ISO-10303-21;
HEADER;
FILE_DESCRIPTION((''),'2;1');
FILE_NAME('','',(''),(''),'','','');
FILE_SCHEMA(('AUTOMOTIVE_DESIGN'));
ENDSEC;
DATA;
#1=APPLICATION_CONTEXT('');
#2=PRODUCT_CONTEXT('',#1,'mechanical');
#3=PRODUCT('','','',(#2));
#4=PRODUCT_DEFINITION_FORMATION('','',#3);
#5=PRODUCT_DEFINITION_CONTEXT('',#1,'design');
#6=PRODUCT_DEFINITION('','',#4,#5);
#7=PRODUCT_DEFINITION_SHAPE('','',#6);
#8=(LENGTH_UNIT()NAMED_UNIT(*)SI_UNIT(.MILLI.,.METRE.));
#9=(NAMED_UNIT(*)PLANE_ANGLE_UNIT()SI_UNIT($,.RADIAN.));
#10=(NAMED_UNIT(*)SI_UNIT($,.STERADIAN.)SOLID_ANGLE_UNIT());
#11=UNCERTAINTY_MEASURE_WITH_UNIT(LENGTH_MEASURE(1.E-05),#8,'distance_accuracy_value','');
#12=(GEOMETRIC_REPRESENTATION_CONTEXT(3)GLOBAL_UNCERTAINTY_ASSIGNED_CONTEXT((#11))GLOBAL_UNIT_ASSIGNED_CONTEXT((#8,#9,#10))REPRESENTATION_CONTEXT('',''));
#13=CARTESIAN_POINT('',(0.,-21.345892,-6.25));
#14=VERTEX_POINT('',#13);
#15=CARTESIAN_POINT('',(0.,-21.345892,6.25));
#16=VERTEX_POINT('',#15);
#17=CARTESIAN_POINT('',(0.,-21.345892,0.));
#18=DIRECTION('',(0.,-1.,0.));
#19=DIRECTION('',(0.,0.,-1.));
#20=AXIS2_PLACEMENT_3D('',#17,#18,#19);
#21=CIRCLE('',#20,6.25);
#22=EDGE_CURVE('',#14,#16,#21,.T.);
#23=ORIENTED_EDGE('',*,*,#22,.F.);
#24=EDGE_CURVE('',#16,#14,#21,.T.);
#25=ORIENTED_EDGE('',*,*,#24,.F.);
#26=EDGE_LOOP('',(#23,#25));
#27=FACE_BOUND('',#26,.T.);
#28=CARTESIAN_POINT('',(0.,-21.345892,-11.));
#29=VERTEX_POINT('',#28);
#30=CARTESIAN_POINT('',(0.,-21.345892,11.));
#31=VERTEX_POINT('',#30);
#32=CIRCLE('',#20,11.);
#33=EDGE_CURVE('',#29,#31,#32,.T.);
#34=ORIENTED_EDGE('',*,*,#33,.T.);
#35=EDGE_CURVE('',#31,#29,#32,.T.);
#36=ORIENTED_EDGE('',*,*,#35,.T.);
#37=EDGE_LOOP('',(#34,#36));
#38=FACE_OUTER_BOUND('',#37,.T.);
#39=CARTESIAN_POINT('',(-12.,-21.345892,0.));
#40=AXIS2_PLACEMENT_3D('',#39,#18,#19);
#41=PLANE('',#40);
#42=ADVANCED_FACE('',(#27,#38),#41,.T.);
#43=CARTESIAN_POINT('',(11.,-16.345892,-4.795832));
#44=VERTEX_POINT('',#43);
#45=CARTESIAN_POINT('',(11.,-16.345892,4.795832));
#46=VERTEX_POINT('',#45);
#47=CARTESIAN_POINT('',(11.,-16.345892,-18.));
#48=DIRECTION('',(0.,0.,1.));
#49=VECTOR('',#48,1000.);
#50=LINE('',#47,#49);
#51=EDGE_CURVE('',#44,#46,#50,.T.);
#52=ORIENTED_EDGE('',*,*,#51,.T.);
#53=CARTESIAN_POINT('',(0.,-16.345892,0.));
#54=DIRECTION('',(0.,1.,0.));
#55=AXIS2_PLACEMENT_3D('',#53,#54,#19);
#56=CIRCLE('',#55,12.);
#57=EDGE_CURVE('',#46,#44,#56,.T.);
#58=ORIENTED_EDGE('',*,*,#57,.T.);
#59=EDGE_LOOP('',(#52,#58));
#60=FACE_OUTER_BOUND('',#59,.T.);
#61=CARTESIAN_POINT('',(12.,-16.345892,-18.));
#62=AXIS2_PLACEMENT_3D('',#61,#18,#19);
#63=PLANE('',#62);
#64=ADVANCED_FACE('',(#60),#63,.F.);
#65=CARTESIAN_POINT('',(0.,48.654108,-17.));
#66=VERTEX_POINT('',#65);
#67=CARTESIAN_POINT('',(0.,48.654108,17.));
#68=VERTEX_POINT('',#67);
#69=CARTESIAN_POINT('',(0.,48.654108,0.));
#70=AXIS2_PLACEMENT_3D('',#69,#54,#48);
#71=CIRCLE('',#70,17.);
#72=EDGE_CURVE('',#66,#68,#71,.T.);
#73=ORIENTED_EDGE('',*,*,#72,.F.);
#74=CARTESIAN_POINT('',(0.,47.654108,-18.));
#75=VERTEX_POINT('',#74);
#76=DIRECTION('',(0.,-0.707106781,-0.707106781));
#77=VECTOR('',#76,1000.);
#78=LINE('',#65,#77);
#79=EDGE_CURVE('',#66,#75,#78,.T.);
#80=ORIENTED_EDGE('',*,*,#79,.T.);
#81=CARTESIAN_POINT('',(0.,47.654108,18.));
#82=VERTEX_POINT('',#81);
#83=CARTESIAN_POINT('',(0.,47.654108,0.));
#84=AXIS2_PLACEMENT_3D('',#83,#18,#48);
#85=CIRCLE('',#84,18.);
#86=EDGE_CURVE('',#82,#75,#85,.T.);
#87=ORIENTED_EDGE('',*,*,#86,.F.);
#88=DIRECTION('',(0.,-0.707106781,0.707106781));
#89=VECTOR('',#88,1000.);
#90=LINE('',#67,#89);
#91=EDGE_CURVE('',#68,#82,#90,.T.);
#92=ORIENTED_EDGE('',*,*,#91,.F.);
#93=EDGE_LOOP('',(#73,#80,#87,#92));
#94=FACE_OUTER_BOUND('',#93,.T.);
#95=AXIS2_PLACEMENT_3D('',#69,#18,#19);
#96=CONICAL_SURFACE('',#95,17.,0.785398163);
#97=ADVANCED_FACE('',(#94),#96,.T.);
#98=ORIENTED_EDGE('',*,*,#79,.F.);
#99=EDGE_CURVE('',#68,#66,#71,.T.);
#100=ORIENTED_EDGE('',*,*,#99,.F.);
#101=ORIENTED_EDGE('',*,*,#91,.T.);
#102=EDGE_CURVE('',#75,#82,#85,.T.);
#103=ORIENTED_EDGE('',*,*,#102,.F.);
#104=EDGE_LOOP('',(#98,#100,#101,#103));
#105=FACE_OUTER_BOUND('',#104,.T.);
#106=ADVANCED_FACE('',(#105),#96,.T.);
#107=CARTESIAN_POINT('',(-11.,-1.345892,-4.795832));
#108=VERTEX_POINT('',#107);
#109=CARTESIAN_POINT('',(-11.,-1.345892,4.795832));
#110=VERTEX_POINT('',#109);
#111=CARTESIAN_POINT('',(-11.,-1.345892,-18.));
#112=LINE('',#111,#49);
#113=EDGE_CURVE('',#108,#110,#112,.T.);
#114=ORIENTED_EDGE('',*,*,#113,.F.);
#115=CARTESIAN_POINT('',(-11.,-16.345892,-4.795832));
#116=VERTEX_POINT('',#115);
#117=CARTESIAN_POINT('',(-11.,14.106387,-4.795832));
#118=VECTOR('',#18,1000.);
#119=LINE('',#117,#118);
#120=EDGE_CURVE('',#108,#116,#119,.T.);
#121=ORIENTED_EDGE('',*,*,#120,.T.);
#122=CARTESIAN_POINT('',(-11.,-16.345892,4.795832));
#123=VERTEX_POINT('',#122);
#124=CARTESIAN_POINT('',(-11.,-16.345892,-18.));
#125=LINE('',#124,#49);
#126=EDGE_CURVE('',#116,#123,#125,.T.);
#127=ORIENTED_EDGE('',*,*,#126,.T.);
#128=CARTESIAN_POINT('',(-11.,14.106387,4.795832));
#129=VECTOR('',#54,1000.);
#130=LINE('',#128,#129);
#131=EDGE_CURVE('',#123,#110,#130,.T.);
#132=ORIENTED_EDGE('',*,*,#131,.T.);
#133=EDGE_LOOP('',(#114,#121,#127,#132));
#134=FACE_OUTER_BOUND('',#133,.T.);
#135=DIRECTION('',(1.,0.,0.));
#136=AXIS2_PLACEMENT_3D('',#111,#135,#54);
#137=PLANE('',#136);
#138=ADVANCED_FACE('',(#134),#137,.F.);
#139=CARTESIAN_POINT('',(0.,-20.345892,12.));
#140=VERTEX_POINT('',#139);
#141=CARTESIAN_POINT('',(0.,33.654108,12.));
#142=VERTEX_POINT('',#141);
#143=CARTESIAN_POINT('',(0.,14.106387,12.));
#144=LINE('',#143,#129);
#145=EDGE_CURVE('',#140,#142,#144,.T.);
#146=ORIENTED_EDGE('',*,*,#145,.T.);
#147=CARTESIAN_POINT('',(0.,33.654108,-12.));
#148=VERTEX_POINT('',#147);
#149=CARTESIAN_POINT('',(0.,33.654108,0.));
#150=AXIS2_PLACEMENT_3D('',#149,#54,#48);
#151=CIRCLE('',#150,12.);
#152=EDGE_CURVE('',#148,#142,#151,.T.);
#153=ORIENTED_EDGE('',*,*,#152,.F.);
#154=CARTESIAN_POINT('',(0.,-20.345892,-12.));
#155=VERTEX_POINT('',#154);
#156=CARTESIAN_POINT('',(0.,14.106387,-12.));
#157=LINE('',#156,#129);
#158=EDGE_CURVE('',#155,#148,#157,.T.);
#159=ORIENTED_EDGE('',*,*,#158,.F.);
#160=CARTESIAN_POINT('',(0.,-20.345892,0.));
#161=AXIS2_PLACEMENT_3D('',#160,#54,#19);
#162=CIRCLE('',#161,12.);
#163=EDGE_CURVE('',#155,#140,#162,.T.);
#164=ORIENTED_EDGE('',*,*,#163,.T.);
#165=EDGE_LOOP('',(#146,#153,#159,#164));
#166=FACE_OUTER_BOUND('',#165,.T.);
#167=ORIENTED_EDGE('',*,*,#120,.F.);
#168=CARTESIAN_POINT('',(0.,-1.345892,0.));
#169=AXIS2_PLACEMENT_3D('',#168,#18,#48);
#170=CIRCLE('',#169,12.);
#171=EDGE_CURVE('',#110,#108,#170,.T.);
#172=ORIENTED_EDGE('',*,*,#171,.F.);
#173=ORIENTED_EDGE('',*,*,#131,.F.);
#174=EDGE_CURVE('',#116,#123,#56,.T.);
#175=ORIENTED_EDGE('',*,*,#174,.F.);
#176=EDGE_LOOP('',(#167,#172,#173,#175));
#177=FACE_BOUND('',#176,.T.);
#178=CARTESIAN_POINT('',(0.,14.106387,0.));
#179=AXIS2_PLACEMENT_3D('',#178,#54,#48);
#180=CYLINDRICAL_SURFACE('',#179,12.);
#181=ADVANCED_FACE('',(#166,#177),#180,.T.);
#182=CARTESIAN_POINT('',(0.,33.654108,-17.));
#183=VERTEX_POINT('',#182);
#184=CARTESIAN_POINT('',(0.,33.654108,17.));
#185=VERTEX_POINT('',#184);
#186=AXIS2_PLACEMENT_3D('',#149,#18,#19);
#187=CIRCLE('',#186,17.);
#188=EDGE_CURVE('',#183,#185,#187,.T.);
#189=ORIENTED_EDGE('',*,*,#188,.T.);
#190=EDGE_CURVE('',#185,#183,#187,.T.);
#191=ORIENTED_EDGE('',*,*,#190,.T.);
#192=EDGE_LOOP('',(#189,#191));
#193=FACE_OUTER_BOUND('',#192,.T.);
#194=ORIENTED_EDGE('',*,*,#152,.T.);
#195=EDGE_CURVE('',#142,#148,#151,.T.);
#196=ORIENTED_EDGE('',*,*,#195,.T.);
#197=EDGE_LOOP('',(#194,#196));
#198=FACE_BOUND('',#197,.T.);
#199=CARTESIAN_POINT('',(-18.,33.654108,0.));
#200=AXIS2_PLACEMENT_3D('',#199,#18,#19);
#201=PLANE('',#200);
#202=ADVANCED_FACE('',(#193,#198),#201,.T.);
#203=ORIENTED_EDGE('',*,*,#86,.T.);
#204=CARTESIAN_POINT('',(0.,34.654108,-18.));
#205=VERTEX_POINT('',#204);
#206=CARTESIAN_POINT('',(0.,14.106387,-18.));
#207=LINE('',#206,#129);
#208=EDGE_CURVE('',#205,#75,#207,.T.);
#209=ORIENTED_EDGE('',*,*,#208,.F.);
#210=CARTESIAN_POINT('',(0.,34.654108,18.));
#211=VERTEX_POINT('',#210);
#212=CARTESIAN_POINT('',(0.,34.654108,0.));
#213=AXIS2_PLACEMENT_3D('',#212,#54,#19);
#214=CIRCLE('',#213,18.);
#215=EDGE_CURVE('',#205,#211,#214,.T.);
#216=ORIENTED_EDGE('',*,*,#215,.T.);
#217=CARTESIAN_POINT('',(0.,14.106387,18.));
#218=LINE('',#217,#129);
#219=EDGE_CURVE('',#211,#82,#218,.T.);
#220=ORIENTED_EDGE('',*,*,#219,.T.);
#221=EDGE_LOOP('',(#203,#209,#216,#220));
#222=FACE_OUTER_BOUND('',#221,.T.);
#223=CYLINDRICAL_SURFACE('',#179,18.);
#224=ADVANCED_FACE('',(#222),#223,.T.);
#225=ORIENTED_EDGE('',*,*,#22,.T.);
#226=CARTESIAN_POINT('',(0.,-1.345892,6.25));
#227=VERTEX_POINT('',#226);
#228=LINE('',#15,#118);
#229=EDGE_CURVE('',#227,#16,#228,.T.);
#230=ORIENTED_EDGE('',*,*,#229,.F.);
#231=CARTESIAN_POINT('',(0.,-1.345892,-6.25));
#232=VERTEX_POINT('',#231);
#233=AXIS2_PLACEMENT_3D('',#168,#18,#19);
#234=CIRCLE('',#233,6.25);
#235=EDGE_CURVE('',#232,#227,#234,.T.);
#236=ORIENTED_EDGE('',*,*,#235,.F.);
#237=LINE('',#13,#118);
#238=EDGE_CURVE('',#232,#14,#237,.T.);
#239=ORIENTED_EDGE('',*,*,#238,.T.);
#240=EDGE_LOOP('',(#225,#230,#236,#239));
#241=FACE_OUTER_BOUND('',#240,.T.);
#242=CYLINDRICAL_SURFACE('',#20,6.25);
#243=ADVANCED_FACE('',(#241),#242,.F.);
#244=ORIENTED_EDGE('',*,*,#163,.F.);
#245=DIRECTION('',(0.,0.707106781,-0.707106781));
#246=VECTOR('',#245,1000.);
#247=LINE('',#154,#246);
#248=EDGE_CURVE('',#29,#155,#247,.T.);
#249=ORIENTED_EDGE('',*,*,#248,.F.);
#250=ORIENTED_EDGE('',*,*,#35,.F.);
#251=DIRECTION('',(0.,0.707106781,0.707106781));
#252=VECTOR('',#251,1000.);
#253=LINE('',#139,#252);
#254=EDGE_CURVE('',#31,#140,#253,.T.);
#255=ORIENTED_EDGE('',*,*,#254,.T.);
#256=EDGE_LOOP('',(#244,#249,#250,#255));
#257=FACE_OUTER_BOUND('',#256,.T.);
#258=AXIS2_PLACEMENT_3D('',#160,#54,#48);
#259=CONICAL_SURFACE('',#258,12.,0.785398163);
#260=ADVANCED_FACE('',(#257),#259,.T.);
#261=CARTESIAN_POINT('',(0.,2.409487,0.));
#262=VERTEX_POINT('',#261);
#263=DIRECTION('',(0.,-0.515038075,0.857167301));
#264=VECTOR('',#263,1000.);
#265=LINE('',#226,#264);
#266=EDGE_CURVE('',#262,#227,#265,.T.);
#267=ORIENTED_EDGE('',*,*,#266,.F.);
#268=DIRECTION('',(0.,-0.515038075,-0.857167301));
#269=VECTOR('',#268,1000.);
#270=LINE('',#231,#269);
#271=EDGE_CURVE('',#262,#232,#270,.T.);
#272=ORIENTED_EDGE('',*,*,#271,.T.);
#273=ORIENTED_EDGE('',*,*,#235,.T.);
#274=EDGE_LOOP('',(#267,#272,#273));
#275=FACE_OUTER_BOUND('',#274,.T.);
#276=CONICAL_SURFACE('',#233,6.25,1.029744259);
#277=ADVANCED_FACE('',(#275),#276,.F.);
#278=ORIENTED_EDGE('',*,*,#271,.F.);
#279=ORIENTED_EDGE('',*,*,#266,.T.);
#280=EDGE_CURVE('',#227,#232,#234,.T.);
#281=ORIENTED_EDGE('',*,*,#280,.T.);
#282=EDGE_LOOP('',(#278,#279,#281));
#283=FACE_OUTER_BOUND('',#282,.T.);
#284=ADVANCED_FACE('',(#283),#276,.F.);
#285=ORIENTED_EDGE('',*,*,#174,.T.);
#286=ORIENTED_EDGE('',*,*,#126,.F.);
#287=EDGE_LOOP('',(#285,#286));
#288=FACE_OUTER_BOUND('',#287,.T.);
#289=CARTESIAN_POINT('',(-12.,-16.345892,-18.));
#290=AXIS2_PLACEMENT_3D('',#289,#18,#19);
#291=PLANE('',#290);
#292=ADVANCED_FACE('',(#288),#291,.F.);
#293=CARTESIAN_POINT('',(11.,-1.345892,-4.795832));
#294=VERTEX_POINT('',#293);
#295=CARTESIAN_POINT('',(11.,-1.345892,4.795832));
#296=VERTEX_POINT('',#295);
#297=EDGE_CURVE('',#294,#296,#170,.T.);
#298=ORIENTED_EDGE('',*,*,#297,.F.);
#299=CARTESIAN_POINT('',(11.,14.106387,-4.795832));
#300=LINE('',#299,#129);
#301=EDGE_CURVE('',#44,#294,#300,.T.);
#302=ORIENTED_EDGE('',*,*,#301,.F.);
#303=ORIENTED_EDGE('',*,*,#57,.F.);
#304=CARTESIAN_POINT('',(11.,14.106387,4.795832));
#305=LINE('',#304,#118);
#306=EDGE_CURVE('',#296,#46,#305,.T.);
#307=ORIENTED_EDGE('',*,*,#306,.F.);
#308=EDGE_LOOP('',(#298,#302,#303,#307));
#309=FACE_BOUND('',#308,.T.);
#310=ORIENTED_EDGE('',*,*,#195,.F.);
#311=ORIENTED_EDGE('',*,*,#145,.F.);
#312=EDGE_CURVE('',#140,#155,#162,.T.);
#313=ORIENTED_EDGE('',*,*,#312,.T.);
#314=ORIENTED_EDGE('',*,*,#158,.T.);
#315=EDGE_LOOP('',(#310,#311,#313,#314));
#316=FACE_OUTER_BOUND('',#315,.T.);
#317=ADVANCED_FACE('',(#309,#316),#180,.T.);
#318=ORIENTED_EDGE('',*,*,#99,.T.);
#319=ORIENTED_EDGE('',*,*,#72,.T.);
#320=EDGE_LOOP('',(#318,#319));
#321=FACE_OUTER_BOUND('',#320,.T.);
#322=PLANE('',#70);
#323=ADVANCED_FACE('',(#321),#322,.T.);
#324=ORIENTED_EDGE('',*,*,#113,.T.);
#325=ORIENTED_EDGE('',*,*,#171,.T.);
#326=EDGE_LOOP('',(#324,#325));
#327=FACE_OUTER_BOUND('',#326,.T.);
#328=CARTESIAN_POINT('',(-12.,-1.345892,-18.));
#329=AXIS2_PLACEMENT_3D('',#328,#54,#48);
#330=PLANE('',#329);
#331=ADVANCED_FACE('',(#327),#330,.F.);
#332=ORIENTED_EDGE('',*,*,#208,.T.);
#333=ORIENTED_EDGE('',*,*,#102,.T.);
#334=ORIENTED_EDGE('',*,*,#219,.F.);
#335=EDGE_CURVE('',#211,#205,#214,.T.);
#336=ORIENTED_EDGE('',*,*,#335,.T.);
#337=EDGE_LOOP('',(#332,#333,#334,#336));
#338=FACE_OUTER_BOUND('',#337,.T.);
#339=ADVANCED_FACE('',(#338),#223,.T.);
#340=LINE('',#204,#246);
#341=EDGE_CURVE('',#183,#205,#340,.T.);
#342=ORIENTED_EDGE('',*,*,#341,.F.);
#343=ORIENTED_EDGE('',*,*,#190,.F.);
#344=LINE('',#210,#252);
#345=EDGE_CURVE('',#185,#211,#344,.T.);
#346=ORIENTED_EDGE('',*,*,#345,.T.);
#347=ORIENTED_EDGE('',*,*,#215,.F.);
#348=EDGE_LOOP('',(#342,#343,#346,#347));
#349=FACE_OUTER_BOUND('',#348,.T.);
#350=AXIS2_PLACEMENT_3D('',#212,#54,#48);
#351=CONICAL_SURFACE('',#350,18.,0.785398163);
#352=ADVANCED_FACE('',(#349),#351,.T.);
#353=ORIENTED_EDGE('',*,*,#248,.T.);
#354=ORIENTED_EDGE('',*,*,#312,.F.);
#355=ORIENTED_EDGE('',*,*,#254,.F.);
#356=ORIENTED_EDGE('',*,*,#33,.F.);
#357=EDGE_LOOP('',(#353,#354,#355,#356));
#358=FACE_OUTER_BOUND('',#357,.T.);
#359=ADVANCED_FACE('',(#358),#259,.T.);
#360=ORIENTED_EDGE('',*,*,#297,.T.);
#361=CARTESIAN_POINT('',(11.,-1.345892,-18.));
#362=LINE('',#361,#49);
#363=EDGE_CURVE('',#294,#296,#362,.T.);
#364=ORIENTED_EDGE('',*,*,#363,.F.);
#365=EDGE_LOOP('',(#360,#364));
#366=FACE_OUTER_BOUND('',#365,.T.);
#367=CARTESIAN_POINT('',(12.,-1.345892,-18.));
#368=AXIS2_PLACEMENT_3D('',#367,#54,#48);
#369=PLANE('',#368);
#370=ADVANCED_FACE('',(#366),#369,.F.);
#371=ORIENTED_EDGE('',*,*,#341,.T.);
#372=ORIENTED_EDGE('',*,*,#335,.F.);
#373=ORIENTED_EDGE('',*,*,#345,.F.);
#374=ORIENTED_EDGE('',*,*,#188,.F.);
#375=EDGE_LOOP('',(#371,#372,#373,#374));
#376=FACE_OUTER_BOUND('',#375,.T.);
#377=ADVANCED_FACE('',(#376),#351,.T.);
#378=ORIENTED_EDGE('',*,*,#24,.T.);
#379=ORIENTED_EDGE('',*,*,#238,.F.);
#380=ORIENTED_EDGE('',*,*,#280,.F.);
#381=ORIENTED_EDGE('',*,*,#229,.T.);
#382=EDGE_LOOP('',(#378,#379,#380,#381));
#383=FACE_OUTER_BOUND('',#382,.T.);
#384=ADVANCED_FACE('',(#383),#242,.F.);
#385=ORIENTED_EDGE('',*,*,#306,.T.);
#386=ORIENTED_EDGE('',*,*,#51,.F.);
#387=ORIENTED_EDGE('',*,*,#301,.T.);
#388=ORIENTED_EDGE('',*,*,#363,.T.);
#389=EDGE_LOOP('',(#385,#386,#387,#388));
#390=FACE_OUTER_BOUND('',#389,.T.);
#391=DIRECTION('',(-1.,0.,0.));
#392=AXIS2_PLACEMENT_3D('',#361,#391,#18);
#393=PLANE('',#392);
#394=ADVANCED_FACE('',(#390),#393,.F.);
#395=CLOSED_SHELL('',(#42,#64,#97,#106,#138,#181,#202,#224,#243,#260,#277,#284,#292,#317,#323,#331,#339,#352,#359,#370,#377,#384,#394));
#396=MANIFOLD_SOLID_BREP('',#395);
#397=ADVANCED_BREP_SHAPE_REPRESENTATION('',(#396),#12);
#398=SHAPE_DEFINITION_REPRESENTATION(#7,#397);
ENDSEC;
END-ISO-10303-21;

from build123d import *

# Parameters (mm, degrees)
CHAMFER1_SIZE              = 1
CUT_EXTRUDE1_DEPTH         = 55.911039474
CUT_EXTRUDE1_DEPTH_BACK    = 55.911039474
SKETCH3_W                  = 1
SKETCH3_H                  = 15
M14X1_5_TAPPED_HOLE1_D     = 12.5
M14X1_5_TAPPED_HOLE1_DEPTH = 20
M14X1_5_TAPPED_HOLE1_TIP   = 3.755378869


with BuildPart() as part:
    # Sketch2 → Revolve1 (revolve)
    with BuildSketch(Plane.XY, mode=Mode.PRIVATE) as revolve1_sk:
        Polygon((0, 48.654108317), (-18, 48.654108317), (-18, 33.654108317), (-12, 33.654108317), (-12, -21.345891683), (0, -21.345891683), align=None)
    revolve(revolve1_sk.sketch.rotate(Axis((0, 14.106387272, 0), (0, -1, 0)), 270), axis=Axis((0, 14.106387272, 0), (0, -1, 0)))

    # Chamfer1
    chamfer1_edges = [part.edges().sort_by_distance(p)[0] for p in [
        (0, -21.345891683, -12),
        (0, 33.654108317, -18),
        (0, 48.654108317, -18),
    ]]
    chamfer(chamfer1_edges, length=CHAMFER1_SIZE)

    # Sketch3 → Cut-Extrude1 (cut, two sides: drawn at the far end of the back side and taken through both)
    with BuildSketch(Plane.XY.offset(-CUT_EXTRUDE1_DEPTH_BACK)):
        with Locations((-11.5, -8.845891683)):
            Rectangle(SKETCH3_W, SKETCH3_H)
        with Locations((11.5, -8.845891683)):
            Rectangle(SKETCH3_W, SKETCH3_H)
    extrude(amount=CUT_EXTRUDE1_DEPTH + CUT_EXTRUDE1_DEPTH_BACK, mode=Mode.SUBTRACT)

    # M14x1.5 Tapped Hole1
    with Locations(Plane(origin=(0, -21.345891683, 0), x_dir=(-1, 0, 0), z_dir=(0, -1, 0))):
        with Locations((0, 0)):
            Hole(M14X1_5_TAPPED_HOLE1_D / 2, depth=M14X1_5_TAPPED_HOLE1_DEPTH)
            with Locations((0, 0, -(M14X1_5_TAPPED_HOLE1_DEPTH + M14X1_5_TAPPED_HOLE1_TIP / 2))):  # 118° drill point
                Cone(0, M14X1_5_TAPPED_HOLE1_D / 2, M14X1_5_TAPPED_HOLE1_TIP, mode=Mode.SUBTRACT)


solid = part.part
